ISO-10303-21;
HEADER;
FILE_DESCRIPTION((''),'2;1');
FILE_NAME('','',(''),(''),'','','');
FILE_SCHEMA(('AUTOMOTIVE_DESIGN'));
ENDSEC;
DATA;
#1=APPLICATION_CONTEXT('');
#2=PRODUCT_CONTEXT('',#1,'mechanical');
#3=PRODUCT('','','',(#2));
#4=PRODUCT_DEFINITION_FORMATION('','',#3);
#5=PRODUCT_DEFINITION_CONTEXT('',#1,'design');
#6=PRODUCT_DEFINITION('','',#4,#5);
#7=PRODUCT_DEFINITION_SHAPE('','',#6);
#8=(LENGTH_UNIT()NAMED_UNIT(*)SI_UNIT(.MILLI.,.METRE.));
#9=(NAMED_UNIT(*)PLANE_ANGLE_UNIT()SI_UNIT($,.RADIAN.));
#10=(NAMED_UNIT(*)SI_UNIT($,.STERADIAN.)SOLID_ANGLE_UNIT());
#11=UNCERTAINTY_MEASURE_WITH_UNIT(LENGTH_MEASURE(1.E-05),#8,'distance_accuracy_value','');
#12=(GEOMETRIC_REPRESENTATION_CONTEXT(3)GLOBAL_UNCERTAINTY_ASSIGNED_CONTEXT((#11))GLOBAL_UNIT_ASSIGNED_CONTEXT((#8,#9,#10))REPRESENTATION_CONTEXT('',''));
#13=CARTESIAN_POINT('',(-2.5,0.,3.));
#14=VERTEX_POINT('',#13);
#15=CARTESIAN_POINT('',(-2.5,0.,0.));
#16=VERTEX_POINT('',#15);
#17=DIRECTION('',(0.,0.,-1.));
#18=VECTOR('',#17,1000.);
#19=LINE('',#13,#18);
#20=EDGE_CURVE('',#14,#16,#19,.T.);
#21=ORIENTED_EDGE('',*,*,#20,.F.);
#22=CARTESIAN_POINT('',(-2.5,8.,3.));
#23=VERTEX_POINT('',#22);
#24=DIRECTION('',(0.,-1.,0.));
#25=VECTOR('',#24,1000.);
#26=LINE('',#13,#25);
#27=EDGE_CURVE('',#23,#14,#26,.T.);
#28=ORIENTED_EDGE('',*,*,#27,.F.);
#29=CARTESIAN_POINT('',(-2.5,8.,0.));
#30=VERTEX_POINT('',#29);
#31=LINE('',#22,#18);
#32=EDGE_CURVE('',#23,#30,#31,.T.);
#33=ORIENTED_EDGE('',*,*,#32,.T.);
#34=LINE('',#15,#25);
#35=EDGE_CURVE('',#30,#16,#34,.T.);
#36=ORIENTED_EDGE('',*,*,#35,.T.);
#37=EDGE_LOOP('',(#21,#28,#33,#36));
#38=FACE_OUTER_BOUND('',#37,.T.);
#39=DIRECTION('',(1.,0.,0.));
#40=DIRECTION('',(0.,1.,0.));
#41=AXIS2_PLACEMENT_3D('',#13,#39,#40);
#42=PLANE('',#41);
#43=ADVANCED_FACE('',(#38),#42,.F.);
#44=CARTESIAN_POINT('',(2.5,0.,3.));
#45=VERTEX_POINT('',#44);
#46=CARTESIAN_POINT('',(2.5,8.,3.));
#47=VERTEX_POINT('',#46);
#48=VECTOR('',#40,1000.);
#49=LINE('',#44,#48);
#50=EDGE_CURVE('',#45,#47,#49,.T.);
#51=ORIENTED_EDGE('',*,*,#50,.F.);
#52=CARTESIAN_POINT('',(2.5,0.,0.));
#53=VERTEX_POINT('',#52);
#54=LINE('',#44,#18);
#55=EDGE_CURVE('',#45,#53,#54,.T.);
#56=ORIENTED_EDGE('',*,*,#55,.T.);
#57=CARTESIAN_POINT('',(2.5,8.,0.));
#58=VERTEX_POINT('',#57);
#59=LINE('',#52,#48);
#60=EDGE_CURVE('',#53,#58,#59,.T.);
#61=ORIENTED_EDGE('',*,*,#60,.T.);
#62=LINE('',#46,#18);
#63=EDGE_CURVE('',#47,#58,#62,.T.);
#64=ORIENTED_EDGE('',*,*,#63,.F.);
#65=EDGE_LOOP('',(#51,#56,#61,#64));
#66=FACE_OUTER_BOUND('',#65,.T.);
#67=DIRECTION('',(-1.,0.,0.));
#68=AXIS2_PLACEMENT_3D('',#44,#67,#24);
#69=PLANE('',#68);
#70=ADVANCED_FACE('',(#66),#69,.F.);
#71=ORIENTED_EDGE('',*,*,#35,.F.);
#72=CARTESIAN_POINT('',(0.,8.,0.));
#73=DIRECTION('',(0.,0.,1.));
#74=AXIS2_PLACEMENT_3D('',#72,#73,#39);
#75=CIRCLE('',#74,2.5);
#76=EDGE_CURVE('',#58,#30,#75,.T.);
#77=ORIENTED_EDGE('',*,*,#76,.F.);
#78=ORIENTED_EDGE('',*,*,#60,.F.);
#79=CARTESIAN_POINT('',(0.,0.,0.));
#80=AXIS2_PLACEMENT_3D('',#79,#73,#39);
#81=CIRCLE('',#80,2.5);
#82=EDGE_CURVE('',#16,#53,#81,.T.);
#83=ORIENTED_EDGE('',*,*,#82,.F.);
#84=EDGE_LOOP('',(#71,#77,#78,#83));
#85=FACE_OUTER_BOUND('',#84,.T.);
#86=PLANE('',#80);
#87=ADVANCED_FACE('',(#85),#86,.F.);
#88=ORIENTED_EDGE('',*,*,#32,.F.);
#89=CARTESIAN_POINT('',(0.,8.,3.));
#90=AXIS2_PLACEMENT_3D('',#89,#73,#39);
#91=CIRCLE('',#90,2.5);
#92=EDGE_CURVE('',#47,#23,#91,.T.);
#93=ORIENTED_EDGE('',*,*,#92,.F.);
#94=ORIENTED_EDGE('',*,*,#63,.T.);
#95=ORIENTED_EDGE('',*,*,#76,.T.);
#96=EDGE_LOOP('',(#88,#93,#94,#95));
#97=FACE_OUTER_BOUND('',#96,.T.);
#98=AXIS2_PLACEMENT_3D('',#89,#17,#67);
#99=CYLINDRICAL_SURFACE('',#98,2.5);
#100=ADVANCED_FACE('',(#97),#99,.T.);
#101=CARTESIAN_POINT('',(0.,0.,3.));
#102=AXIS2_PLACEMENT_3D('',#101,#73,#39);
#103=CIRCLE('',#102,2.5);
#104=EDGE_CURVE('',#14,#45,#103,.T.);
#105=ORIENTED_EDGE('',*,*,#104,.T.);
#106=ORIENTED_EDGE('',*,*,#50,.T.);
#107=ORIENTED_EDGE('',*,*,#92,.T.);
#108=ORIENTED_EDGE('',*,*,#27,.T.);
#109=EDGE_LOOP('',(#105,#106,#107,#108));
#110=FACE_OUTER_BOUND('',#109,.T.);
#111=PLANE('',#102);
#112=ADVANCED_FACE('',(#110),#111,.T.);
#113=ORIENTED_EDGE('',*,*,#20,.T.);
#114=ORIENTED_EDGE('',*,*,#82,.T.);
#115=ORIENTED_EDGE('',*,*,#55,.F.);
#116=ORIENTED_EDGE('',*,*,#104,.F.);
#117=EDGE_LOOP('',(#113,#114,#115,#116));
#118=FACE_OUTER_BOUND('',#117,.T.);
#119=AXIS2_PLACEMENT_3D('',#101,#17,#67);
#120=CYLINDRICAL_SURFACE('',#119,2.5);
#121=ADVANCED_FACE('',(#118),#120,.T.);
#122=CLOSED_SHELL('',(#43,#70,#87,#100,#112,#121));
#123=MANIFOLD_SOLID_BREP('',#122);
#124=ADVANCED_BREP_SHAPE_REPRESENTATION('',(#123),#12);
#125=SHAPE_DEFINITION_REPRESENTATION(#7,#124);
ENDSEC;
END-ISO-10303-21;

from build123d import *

# Parameters (mm, degrees)
KEY_BODY_3MM_DEPTH = 3


with BuildPart() as part:
    # Key Profile 5x13 → Key Body 3mm (new body)
    with BuildSketch(Plane.XY):
        with BuildLine():
            Line((-2.5, 0), (-2.5, 8))
            ThreePointArc((-2.5, 8), (0, 10.5), (2.5, 8))
            Line((2.5, 8), (2.5, 0))
            ThreePointArc((2.5, 0), (0, -2.5), (-2.5, 0))
        make_face()
    extrude(amount=KEY_BODY_3MM_DEPTH)


solid = part.part
